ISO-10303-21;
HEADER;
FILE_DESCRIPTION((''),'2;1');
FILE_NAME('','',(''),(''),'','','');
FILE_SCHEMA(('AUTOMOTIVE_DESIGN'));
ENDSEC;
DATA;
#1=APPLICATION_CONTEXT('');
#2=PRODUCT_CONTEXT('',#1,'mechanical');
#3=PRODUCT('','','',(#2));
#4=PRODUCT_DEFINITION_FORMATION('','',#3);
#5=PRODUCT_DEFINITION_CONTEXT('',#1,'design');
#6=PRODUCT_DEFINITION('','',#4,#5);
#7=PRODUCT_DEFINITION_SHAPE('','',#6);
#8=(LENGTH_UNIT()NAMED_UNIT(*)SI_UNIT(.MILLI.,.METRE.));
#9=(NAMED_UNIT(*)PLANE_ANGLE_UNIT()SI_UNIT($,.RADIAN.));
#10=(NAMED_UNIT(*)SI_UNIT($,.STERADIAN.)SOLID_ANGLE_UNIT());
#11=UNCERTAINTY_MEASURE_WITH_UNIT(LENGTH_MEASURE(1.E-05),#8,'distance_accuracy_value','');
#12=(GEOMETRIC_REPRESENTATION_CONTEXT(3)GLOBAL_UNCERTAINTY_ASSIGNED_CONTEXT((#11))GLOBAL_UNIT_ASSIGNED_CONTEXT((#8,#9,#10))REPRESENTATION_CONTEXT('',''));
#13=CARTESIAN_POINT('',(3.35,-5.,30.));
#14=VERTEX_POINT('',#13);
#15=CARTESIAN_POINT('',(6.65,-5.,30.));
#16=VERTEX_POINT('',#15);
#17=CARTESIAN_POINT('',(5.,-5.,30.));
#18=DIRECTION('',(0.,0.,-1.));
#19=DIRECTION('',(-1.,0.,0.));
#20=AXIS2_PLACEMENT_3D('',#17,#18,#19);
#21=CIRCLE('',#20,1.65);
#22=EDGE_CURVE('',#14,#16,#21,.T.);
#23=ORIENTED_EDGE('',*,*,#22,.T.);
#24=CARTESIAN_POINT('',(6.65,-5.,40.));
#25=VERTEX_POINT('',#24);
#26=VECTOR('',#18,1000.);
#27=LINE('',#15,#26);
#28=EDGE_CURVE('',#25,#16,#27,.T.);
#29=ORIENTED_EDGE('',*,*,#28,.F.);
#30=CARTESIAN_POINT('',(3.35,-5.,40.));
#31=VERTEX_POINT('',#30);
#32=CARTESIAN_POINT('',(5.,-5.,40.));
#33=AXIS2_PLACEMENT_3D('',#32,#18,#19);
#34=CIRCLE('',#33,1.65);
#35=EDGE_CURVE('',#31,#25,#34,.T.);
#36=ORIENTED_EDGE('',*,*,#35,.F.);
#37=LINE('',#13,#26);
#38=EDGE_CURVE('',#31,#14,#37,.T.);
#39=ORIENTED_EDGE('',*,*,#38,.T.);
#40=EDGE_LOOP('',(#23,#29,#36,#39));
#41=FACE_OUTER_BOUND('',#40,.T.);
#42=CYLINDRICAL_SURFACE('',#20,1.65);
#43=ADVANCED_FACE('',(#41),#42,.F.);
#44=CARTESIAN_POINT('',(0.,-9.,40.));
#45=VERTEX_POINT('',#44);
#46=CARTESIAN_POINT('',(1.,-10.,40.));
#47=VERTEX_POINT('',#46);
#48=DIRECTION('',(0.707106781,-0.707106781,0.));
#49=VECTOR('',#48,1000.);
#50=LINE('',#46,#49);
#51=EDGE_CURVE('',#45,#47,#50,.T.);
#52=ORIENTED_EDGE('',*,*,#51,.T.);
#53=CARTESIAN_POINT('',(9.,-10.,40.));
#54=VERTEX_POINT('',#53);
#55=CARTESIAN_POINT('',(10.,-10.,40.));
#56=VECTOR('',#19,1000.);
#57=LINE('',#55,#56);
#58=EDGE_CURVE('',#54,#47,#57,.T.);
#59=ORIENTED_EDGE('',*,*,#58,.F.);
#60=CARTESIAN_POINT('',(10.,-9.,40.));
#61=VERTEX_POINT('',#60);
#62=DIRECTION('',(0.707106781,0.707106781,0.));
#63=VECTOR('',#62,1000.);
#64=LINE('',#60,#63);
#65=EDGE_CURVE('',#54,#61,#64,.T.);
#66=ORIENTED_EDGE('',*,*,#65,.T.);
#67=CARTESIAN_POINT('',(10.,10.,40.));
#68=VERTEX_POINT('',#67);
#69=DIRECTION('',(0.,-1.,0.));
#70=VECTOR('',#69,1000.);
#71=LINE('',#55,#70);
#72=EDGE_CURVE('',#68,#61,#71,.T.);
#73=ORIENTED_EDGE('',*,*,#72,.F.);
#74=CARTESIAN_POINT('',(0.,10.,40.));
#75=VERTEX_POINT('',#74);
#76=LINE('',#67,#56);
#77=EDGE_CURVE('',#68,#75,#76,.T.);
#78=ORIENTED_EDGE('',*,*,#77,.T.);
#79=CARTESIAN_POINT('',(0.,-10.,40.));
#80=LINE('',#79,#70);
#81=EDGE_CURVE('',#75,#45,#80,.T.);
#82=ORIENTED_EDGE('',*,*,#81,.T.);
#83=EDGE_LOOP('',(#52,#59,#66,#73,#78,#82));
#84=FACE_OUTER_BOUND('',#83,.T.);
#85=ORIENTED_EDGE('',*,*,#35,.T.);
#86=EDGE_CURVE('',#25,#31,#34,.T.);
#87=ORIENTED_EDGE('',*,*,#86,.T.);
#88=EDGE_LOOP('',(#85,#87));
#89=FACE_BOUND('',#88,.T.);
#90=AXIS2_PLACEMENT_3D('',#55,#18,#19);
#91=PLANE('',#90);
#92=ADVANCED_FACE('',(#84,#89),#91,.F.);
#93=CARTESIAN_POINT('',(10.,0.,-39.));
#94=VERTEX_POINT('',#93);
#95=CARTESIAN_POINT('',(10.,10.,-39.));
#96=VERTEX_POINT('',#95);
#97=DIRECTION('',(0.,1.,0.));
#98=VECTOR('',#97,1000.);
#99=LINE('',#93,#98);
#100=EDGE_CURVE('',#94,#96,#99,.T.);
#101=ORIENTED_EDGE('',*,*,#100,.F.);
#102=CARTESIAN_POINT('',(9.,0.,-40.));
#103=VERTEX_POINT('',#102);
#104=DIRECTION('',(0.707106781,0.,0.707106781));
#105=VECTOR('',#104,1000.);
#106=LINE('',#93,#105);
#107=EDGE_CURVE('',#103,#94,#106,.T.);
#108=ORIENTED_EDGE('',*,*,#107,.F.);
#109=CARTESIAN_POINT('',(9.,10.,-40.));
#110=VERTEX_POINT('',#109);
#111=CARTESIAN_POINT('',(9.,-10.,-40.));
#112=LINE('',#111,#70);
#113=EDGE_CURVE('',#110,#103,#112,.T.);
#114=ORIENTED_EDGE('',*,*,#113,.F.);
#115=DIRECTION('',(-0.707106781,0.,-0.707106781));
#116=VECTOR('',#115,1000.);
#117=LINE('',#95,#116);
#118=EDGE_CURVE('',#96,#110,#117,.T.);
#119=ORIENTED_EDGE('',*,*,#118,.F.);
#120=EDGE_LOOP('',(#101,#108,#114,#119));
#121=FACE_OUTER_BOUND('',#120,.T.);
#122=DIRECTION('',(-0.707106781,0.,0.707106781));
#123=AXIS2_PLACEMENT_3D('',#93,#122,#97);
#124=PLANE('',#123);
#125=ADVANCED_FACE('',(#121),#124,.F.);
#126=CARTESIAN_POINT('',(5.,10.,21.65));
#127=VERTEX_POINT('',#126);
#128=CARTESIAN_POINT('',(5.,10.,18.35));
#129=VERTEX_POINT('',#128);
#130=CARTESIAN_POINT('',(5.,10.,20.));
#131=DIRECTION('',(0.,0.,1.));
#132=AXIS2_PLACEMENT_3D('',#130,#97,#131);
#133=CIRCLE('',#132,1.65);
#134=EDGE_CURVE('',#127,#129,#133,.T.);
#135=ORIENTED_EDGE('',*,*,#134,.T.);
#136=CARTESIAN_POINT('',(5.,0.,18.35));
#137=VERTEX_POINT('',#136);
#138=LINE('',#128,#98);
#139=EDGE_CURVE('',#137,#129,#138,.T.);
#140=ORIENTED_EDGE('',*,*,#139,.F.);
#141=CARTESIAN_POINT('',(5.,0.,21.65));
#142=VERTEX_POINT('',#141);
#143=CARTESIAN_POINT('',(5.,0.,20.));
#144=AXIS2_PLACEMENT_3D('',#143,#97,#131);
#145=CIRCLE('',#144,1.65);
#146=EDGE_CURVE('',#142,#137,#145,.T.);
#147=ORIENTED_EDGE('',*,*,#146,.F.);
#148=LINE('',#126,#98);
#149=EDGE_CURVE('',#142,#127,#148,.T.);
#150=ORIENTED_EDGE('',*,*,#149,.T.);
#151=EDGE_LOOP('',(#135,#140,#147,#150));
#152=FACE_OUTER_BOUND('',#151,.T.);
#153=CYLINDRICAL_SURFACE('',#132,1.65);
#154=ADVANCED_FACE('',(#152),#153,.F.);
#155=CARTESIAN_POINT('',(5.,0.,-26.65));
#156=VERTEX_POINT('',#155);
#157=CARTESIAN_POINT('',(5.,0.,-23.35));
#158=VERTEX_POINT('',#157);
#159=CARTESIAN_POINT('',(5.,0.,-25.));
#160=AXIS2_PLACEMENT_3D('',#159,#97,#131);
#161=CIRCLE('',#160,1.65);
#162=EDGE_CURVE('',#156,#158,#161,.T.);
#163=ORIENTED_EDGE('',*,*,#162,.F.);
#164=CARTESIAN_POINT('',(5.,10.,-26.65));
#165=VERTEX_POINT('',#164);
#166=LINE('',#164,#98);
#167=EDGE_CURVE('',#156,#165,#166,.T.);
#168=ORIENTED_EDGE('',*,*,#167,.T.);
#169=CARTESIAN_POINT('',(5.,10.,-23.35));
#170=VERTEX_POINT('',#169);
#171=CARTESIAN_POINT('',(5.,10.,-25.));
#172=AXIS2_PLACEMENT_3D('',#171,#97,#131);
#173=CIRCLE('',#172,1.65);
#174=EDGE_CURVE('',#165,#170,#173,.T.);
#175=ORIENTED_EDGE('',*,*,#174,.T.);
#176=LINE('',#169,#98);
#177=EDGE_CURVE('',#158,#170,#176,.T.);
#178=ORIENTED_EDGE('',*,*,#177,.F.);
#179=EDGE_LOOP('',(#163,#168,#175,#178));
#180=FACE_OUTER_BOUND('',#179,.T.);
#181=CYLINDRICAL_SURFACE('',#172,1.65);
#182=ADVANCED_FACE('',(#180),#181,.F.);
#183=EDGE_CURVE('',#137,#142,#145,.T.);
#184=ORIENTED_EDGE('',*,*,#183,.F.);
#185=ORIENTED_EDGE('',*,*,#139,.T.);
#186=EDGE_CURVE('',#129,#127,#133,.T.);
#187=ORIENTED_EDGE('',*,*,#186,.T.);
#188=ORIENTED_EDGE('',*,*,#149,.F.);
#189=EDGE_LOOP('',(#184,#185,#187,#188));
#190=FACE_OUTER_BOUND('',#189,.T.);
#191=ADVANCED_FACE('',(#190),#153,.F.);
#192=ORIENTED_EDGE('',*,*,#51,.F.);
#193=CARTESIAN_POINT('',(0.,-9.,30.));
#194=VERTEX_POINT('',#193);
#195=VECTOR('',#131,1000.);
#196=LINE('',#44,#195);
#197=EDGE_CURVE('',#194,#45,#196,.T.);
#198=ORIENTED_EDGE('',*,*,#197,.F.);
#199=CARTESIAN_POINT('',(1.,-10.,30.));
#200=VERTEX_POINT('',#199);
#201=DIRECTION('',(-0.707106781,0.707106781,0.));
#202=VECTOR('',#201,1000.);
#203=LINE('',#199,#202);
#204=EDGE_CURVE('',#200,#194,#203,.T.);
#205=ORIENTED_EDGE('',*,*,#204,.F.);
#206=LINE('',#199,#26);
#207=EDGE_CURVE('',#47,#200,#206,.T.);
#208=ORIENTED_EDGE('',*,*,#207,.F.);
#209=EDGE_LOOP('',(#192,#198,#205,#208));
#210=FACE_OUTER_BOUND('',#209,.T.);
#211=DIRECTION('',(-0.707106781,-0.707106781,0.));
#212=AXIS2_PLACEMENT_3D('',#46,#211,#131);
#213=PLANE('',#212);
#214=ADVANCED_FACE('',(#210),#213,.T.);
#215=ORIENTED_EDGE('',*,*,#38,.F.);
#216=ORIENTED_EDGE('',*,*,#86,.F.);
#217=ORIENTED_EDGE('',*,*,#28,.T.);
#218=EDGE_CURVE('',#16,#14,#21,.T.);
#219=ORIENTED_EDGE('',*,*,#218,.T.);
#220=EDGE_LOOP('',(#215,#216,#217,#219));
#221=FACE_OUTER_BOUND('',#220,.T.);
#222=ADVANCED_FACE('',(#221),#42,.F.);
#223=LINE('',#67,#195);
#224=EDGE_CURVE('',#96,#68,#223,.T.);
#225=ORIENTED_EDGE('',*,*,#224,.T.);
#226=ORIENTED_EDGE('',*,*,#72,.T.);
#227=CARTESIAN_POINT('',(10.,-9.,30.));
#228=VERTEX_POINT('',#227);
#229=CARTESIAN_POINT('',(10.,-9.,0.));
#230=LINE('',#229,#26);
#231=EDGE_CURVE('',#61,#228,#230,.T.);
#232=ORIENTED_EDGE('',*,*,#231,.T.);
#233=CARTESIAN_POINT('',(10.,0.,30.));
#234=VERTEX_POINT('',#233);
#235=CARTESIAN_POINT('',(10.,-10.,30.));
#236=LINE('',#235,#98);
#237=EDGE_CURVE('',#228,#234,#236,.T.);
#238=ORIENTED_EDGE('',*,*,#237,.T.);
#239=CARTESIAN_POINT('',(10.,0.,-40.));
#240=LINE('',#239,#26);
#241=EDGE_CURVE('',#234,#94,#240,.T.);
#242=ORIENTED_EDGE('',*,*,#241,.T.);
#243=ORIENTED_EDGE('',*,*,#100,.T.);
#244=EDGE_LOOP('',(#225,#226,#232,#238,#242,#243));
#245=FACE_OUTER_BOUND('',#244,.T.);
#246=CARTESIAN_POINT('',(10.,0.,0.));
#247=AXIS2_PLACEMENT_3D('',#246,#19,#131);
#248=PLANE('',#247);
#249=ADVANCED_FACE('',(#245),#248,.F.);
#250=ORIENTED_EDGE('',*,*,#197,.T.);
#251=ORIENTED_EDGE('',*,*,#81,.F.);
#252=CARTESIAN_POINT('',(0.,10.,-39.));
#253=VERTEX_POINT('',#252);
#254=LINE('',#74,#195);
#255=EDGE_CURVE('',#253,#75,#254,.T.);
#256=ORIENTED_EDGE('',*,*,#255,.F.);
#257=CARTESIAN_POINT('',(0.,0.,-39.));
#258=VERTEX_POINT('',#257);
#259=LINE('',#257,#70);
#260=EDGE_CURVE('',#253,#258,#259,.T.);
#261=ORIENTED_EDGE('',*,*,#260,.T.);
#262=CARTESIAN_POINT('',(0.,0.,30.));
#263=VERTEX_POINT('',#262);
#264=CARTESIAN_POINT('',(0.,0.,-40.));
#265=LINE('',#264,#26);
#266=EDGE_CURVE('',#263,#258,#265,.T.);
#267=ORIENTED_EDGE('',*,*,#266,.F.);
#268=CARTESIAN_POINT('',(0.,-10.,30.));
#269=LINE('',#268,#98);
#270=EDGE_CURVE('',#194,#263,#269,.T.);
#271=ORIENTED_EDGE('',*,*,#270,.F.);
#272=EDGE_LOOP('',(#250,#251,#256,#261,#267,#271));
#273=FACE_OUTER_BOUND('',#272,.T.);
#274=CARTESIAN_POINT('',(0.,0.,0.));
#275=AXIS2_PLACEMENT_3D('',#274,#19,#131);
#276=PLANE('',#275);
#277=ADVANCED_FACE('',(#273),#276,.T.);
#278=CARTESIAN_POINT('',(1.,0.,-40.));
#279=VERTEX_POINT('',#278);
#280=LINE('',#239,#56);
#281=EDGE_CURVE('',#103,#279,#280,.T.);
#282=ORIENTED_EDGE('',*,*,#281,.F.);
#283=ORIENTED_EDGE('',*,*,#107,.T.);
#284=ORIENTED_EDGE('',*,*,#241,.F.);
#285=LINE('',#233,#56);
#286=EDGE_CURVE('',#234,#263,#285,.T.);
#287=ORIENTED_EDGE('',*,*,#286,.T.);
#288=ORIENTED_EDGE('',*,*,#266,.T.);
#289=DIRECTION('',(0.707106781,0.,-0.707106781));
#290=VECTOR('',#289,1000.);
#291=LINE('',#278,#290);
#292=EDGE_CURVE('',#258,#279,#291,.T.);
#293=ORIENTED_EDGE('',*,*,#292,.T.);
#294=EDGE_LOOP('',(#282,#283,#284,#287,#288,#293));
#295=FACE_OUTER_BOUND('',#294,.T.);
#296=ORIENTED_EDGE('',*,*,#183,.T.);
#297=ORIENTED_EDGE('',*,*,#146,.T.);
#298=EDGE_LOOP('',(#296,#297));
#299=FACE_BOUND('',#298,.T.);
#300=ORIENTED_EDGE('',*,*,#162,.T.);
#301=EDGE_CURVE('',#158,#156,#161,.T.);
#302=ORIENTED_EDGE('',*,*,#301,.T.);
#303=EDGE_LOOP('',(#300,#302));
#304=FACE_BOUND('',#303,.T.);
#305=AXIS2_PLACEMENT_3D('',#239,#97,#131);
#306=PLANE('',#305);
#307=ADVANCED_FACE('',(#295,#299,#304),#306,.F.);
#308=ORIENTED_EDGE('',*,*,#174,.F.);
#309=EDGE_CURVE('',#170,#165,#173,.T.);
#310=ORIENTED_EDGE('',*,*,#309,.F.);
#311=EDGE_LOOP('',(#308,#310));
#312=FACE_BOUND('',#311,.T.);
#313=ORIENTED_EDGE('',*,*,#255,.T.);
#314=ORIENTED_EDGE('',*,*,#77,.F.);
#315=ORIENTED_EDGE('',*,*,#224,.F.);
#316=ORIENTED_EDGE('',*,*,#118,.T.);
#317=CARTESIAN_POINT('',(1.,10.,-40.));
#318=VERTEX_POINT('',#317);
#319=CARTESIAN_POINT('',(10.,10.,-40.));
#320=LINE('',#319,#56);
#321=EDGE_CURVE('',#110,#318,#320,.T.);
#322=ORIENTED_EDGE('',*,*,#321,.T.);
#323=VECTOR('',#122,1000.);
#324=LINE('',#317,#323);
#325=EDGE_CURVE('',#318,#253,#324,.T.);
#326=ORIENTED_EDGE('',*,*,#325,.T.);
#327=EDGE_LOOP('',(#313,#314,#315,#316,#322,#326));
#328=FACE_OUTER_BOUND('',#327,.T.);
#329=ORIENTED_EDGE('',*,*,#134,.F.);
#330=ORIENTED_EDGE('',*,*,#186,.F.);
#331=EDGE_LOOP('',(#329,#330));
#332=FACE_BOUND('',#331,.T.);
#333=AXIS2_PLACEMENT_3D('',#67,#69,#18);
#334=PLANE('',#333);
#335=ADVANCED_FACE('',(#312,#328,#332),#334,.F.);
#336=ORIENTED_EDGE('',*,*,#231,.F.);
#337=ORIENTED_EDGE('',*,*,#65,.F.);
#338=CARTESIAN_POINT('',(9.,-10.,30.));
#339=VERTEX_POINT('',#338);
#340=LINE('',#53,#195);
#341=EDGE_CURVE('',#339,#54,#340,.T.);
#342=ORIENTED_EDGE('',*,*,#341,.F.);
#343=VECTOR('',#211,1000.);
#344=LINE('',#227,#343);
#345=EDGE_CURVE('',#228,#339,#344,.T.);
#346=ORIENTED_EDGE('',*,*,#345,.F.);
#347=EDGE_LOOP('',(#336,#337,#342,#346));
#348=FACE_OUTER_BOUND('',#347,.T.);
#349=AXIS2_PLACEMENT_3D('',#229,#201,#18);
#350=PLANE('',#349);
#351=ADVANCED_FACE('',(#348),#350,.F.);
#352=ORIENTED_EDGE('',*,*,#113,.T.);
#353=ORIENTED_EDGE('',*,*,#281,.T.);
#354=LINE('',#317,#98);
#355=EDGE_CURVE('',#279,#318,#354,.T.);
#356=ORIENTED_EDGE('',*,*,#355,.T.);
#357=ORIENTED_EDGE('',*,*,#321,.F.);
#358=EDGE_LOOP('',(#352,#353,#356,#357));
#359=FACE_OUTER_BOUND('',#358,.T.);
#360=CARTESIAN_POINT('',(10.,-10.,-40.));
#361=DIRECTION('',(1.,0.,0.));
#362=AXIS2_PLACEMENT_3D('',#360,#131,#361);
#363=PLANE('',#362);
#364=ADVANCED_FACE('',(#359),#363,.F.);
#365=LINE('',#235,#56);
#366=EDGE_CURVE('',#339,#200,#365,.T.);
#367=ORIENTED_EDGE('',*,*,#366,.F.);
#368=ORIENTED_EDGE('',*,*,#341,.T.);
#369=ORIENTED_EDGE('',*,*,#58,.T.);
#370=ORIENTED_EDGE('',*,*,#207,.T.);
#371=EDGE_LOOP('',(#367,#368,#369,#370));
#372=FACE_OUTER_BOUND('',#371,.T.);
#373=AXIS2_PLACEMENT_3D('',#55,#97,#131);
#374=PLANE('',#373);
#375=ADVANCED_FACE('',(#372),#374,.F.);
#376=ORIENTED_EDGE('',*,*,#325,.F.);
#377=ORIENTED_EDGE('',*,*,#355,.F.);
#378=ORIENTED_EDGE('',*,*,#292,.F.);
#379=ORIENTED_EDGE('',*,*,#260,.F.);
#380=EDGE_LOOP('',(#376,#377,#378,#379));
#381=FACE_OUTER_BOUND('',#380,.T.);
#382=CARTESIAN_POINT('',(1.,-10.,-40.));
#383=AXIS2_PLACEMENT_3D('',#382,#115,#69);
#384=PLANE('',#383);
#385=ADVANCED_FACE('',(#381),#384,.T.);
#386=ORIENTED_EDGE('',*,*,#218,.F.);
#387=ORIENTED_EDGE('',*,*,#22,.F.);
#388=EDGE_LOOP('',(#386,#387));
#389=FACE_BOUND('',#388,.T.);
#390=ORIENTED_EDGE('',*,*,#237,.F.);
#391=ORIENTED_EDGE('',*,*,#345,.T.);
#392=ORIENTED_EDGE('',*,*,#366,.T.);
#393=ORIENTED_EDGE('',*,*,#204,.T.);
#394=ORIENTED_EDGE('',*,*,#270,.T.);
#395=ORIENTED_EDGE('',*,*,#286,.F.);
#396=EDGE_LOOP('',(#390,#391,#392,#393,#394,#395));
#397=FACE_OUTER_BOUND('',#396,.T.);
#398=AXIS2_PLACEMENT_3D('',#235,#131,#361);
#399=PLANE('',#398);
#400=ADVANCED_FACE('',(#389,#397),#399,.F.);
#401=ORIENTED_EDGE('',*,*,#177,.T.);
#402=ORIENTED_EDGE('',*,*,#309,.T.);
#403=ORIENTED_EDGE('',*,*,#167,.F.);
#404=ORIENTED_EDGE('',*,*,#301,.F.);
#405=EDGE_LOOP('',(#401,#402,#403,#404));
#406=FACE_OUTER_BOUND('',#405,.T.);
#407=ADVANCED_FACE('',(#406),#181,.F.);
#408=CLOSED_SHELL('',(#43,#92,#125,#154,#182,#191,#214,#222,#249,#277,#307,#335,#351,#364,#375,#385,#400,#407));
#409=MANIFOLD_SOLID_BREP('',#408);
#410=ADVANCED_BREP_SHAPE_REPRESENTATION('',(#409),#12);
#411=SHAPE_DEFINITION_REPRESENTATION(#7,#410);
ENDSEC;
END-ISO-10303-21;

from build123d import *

# Parameters (mm, degrees)
SKETCH1_W             = 80
SKETCH1_H             = 20
BOSS_EXTRUDE1_DEPTH   = 10
SKETCH3_W             = 70
SKETCH3_H             = 10
CUT_EXTRUDE1_DEPTH    = 43.426406871
M4_TAPPED_HOLE2_D     = 3.3
M4_TAPPED_HOLE2_DEPTH = 10.1
M4_TAPPED_HOLE2_TIP   = 0.991420021
CHAMFER1_SIZE         = 1
M4_TAPPED_HOLE1_D     = 3.3
M4_TAPPED_HOLE1_DEPTH = 10.1
M4_TAPPED_HOLE1_TIP   = 0.991420021


with BuildPart() as part:
    # Sketch1 → Boss-Extrude1 (new body)
    with BuildSketch(Plane(origin=(0, 0, 0), x_dir=(0, 0, -1), z_dir=(1, 0, 0))):
        Rectangle(SKETCH1_W, SKETCH1_H)
    extrude(amount=BOSS_EXTRUDE1_DEPTH)

    # Sketch3 → Cut-Extrude1 (cut, through all)
    with BuildSketch(Plane.ZY):
        with Locations((-5, -5)):
            Rectangle(SKETCH3_W, SKETCH3_H)
    extrude(amount=-CUT_EXTRUDE1_DEPTH, mode=Mode.SUBTRACT)

    # M4 Tapped Hole2
    with Locations(Plane(origin=(0, 0, 30), x_dir=(-1, 0, 0), z_dir=(0, 0, -1))):
        with Locations((-5, -5)):
            Hole(M4_TAPPED_HOLE2_D / 2, depth=M4_TAPPED_HOLE2_DEPTH)
            with Locations((0, 0, -(M4_TAPPED_HOLE2_DEPTH + M4_TAPPED_HOLE2_TIP / 2))):  # 118° drill point
                Cone(0, M4_TAPPED_HOLE2_D / 2, M4_TAPPED_HOLE2_TIP, mode=Mode.SUBTRACT)

    # Chamfer1
    chamfer1_edges = [part.edges().sort_by_distance(p)[0] for p in [
        (0, 5, -40),
        (10, 5, -40),
        (10, -10, 35),
        (0, -10, 35),
    ]]
    chamfer(chamfer1_edges, length=CHAMFER1_SIZE)

    # M4 Tapped Hole1
    with Locations(Plane(origin=(0, 10, 0), x_dir=(1, 0, 0), z_dir=(0, 1, 0))):
        with Locations((5, 25), (5, -20)):
            Hole(M4_TAPPED_HOLE1_D / 2, depth=M4_TAPPED_HOLE1_DEPTH)
            with Locations((0, 0, -(M4_TAPPED_HOLE1_DEPTH + M4_TAPPED_HOLE1_TIP / 2))):  # 118° drill point
                Cone(0, M4_TAPPED_HOLE1_D / 2, M4_TAPPED_HOLE1_TIP, mode=Mode.SUBTRACT)


solid = part.part
